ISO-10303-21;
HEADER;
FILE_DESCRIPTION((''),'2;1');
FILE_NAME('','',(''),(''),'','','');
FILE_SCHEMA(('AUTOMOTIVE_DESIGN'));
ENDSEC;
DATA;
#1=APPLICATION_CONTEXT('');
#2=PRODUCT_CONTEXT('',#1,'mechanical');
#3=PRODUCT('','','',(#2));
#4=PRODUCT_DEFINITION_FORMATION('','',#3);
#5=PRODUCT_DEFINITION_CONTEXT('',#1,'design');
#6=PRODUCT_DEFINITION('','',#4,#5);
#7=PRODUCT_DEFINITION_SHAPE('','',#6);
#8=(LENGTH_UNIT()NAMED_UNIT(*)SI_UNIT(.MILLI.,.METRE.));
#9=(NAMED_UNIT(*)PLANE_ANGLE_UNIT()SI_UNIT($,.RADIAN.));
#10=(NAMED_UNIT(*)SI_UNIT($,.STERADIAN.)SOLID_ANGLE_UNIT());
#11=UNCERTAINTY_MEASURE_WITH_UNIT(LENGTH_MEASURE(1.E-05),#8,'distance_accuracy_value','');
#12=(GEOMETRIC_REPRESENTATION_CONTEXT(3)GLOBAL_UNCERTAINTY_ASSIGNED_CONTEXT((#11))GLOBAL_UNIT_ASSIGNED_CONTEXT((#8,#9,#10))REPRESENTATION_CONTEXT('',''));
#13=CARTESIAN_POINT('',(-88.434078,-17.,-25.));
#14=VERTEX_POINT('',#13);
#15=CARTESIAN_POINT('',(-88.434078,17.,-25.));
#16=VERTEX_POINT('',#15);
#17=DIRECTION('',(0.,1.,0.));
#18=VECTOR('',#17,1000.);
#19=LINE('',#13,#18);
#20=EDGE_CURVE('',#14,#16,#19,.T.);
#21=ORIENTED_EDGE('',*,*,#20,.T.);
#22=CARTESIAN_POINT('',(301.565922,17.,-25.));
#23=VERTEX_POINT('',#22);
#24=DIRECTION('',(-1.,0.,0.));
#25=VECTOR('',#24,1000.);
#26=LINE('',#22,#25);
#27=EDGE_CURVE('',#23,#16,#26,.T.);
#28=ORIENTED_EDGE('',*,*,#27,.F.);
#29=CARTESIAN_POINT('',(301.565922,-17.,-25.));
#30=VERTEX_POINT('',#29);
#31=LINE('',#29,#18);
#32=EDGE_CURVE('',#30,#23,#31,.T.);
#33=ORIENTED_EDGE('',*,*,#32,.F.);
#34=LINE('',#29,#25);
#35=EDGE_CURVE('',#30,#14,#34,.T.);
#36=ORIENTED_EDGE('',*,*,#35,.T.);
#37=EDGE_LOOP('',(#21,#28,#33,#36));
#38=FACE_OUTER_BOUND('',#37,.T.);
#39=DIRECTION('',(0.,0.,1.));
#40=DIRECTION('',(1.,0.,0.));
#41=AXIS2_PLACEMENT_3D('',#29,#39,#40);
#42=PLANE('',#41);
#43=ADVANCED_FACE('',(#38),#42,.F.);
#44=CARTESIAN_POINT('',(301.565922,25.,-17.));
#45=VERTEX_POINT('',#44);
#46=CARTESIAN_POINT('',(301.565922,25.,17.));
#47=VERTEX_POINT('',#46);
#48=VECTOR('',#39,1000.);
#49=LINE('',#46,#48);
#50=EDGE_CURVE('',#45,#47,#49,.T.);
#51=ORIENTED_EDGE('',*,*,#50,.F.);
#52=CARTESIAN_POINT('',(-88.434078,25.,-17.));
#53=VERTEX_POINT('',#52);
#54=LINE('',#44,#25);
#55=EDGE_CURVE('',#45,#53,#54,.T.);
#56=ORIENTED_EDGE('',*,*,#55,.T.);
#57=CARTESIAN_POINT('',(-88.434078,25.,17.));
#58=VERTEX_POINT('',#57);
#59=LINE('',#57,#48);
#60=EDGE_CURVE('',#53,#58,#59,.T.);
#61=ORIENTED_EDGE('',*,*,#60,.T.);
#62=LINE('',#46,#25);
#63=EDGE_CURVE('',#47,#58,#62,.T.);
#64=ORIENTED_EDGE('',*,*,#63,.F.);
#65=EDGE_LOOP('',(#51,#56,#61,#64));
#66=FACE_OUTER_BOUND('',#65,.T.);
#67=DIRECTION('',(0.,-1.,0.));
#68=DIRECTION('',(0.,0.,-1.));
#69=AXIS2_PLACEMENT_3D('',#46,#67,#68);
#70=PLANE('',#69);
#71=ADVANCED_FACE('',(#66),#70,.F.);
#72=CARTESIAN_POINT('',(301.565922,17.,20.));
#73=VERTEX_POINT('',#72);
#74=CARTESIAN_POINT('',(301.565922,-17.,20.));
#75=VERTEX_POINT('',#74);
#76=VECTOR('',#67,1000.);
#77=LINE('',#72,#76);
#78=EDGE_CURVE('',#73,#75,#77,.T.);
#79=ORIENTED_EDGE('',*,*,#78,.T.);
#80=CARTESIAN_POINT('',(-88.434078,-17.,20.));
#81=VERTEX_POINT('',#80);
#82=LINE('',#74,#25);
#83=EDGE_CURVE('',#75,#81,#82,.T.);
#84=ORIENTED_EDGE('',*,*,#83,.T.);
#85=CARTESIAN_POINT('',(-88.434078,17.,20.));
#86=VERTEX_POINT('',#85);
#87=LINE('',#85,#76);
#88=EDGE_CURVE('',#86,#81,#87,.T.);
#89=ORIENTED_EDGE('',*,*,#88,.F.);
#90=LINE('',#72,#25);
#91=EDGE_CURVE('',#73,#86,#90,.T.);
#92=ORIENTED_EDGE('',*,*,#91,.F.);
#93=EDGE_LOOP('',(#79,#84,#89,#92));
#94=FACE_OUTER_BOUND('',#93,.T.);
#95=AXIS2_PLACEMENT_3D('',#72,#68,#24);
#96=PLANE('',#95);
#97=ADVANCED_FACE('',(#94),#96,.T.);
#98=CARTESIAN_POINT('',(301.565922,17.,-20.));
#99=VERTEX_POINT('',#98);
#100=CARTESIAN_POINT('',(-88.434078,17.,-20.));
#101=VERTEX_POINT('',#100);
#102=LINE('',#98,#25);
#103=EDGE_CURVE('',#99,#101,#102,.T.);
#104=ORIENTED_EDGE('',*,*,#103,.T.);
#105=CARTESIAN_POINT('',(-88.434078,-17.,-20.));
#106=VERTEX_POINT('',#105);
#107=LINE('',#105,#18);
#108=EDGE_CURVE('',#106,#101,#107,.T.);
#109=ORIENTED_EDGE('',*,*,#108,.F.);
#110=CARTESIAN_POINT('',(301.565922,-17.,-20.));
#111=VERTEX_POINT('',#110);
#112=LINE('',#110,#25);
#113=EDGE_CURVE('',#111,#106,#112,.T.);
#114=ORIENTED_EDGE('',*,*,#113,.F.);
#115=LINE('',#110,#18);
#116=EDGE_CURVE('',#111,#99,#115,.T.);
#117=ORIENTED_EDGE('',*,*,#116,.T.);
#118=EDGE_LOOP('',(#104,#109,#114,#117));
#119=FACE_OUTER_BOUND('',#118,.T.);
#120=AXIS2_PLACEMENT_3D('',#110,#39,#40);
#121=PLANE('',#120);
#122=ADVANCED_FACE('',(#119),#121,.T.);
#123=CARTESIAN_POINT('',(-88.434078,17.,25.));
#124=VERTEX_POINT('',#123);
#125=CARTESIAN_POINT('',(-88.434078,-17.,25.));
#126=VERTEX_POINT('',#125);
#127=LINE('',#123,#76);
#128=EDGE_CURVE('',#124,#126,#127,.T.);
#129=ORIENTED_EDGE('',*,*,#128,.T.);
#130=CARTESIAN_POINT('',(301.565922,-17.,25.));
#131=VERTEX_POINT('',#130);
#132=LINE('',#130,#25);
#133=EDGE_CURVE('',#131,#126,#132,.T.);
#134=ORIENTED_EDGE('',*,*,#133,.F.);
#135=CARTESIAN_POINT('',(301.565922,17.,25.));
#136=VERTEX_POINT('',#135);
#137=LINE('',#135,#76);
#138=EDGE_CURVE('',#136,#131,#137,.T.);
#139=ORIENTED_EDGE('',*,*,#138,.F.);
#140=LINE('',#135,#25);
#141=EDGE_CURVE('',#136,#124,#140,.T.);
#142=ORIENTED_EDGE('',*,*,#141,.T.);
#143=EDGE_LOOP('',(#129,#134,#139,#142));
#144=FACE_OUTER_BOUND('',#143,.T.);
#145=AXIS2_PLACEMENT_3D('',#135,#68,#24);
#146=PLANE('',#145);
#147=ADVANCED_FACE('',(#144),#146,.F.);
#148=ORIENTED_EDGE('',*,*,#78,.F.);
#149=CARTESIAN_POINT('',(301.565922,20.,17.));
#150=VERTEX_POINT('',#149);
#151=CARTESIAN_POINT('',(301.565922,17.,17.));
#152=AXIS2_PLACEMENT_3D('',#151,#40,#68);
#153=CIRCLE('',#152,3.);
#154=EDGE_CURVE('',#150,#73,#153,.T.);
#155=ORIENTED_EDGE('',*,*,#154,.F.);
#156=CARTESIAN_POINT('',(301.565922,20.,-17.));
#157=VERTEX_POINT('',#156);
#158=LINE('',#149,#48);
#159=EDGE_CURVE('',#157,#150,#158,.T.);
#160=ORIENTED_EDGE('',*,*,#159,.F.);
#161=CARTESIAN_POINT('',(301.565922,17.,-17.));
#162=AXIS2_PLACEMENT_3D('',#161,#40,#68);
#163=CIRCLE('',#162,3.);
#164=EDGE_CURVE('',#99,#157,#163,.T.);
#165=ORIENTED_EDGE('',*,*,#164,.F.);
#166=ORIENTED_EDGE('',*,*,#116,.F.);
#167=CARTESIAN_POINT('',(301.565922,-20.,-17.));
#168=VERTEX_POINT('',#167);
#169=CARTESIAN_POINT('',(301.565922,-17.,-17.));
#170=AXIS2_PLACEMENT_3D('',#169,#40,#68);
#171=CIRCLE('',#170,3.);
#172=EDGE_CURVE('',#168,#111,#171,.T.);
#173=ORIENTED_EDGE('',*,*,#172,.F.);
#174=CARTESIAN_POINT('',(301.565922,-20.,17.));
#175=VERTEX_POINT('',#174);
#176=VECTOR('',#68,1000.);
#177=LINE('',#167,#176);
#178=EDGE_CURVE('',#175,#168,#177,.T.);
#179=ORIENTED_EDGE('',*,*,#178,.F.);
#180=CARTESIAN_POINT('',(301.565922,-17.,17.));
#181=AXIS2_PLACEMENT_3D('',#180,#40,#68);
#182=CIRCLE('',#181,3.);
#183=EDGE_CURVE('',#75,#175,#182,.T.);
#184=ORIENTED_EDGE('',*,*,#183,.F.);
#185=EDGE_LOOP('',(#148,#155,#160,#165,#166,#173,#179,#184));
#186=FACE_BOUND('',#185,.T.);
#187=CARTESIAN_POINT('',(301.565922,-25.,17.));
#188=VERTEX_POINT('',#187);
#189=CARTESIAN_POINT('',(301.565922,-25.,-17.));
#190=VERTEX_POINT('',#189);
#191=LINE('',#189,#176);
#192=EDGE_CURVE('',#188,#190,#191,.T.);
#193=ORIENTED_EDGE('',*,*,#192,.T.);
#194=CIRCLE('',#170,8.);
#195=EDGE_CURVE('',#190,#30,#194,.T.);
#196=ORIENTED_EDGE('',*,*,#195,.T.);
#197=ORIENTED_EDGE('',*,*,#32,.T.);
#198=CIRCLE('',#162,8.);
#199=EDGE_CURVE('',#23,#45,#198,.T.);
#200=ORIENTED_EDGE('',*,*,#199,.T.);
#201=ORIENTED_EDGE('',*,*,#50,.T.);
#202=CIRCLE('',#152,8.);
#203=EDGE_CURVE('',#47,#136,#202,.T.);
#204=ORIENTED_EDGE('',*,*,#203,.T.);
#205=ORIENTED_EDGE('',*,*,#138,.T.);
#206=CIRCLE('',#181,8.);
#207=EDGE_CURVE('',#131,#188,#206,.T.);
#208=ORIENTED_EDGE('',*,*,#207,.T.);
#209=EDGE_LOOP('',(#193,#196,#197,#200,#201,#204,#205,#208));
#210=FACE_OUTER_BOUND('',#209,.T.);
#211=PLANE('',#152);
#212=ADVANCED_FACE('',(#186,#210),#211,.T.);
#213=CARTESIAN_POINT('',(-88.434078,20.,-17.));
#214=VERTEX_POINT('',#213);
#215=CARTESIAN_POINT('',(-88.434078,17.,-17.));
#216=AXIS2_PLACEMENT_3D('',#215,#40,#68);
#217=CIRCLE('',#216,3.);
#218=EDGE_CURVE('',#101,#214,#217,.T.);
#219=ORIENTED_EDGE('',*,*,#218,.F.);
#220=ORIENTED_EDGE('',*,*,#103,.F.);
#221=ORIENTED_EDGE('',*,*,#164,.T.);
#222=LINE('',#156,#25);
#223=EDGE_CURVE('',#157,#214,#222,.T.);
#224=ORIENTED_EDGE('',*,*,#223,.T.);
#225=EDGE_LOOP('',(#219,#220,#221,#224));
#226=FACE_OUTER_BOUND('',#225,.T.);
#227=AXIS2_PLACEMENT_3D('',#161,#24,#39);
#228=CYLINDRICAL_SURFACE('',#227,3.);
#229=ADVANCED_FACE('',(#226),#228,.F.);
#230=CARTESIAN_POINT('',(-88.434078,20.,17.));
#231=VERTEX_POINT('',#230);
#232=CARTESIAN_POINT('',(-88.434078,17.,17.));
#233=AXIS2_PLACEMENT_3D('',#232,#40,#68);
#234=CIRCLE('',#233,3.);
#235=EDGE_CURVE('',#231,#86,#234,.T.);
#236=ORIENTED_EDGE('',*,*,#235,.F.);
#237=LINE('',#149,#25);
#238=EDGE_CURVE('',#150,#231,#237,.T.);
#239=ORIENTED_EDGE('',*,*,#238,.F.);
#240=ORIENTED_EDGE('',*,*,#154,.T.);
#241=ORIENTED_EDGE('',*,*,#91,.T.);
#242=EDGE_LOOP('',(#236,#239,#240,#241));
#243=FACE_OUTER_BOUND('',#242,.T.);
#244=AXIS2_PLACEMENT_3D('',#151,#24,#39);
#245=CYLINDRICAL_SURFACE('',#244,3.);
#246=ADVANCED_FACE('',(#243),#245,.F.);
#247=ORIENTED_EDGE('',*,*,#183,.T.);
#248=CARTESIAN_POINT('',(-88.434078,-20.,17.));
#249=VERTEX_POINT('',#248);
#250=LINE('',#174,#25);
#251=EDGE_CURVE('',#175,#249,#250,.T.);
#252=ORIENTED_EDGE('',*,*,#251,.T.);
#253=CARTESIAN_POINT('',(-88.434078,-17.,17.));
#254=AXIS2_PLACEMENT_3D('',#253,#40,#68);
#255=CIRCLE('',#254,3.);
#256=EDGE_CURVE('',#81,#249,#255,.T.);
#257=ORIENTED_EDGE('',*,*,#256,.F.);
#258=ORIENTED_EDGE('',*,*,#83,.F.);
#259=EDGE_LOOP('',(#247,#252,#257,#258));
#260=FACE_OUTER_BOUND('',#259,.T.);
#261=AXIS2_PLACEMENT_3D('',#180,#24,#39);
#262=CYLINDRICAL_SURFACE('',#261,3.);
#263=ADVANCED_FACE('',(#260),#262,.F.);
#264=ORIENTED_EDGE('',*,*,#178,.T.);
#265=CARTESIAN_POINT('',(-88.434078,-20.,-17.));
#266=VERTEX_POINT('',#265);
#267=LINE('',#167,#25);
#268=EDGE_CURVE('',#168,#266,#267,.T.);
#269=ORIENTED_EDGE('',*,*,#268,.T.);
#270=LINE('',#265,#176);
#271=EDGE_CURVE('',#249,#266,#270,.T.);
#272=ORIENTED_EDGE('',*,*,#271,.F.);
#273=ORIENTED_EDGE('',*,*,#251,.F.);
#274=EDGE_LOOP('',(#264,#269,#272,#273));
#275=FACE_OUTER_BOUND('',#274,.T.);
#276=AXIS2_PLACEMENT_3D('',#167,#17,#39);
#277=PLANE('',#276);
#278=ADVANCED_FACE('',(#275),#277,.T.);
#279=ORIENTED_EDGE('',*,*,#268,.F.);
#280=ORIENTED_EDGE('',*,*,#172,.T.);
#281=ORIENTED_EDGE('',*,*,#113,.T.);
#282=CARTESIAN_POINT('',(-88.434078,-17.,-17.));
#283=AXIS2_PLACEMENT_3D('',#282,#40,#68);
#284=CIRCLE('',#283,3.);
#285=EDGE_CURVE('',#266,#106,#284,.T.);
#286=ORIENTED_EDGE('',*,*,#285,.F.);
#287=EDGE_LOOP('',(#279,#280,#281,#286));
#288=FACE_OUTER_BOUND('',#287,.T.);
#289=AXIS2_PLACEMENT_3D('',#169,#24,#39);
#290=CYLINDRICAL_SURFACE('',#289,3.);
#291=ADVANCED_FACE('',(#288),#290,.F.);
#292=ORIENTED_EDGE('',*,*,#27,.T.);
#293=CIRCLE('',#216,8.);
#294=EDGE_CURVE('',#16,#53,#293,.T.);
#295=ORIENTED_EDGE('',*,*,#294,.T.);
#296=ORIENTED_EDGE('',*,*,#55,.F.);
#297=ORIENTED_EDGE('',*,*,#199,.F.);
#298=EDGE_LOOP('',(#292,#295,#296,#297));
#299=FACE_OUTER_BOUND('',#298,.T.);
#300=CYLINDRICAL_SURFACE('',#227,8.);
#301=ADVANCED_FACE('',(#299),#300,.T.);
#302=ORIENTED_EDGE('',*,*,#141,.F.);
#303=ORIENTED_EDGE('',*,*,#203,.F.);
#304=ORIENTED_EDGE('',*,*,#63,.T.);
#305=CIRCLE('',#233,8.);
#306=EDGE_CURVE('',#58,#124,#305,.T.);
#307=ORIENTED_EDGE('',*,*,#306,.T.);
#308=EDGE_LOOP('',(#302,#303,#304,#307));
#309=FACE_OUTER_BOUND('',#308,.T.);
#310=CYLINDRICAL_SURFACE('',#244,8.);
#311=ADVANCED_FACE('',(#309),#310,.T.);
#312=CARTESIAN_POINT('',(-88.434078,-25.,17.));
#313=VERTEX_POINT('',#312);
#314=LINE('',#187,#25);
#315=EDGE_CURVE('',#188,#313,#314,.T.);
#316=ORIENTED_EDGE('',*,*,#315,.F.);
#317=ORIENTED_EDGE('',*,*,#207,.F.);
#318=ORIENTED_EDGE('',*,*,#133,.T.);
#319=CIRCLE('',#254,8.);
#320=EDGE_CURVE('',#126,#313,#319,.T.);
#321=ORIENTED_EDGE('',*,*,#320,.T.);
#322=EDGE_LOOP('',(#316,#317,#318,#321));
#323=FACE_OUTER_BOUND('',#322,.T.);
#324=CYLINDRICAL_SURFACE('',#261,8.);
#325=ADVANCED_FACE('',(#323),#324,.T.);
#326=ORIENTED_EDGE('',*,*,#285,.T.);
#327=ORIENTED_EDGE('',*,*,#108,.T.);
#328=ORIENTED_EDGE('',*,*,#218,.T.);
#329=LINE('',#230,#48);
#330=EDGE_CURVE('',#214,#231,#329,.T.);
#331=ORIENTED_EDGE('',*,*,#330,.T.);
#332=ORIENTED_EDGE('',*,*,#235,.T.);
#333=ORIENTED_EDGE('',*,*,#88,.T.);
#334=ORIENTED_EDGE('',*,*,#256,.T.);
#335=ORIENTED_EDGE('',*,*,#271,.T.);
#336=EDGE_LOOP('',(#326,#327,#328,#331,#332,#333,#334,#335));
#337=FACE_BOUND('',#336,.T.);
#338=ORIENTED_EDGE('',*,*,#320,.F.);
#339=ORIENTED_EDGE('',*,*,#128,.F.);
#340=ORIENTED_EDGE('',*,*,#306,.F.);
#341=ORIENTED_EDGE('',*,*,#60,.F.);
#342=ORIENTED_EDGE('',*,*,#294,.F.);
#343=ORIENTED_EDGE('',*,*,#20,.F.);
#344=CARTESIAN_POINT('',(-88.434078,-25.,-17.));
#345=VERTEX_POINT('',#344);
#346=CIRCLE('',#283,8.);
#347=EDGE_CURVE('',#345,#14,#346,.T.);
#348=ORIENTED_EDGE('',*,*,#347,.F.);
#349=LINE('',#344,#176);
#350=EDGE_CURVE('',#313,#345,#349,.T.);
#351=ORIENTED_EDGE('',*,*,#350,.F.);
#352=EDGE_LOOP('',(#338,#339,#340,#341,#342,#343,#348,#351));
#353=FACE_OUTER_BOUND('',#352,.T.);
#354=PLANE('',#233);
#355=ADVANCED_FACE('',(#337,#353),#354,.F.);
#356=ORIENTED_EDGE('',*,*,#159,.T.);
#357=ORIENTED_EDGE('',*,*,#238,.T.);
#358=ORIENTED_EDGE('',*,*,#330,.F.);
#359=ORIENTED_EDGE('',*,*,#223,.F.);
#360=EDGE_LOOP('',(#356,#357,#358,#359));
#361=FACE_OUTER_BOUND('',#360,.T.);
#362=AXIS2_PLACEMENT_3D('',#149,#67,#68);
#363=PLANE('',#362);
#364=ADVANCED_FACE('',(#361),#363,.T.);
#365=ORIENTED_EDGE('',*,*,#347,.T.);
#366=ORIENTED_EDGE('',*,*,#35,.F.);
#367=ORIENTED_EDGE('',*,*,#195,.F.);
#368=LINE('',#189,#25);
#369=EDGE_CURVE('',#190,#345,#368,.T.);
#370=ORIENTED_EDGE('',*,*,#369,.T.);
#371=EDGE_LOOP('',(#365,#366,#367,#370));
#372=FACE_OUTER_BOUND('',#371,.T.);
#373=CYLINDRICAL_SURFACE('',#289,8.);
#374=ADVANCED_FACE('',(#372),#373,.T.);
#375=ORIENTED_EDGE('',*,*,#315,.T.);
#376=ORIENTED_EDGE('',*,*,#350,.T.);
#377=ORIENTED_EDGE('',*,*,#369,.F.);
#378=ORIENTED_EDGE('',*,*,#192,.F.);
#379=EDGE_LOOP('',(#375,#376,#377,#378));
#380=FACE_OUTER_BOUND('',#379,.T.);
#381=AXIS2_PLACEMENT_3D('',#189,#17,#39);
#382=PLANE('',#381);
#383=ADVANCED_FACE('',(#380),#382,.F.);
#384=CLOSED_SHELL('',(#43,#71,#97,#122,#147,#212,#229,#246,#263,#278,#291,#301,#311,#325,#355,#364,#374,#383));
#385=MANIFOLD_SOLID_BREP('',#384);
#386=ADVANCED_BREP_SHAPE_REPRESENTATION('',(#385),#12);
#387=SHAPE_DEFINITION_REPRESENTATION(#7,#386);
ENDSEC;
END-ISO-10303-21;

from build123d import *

# Parameters (mm, degrees)
COLD_FORMED_SQUARE_HOLLOW_SECTION_GB_T_6_DEPTH = 390


with BuildPart() as part:
    # Sketch1 → Cold-formed square hollow section GB/T 6728-2002 50 X 50 X 4(1) (new body)
    with BuildSketch(Plane.YZ.offset(-88.434077868)):
        with BuildLine():
            Line((-17, -25), (17, -25))
            ThreePointArc((17, -25), (22.656854249, -22.656854249), (25, -17))
            Line((25, -17), (25, 17))
            ThreePointArc((25, 17), (22.656854249, 22.656854249), (17, 25))
            Line((17, 25), (-17, 25))
            ThreePointArc((-17, 25), (-22.656854249, 22.656854249), (-25, 17))
            Line((-25, 17), (-25, -17))
            ThreePointArc((-25, -17), (-22.656854249, -22.656854249), (-17, -25))
        make_face()
        with BuildLine():
            Line((-17, -20), (17, -20))
            ThreePointArc((17, -20), (19.121320344, -19.121320344), (20, -17))
            Line((20, -17), (20, 17))
            ThreePointArc((20, 17), (19.121320344, 19.121320344), (17, 20))
            Line((17, 20), (-17, 20))
            ThreePointArc((-17, 20), (-19.121320344, 19.121320344), (-20, 17))
            Line((-20, 17), (-20, -17))
            ThreePointArc((-20, -17), (-19.121320344, -19.121320344), (-17, -20))
        make_face(mode=Mode.SUBTRACT)
    extrude(amount=COLD_FORMED_SQUARE_HOLLOW_SECTION_GB_T_6_DEPTH)


solid = part.part
